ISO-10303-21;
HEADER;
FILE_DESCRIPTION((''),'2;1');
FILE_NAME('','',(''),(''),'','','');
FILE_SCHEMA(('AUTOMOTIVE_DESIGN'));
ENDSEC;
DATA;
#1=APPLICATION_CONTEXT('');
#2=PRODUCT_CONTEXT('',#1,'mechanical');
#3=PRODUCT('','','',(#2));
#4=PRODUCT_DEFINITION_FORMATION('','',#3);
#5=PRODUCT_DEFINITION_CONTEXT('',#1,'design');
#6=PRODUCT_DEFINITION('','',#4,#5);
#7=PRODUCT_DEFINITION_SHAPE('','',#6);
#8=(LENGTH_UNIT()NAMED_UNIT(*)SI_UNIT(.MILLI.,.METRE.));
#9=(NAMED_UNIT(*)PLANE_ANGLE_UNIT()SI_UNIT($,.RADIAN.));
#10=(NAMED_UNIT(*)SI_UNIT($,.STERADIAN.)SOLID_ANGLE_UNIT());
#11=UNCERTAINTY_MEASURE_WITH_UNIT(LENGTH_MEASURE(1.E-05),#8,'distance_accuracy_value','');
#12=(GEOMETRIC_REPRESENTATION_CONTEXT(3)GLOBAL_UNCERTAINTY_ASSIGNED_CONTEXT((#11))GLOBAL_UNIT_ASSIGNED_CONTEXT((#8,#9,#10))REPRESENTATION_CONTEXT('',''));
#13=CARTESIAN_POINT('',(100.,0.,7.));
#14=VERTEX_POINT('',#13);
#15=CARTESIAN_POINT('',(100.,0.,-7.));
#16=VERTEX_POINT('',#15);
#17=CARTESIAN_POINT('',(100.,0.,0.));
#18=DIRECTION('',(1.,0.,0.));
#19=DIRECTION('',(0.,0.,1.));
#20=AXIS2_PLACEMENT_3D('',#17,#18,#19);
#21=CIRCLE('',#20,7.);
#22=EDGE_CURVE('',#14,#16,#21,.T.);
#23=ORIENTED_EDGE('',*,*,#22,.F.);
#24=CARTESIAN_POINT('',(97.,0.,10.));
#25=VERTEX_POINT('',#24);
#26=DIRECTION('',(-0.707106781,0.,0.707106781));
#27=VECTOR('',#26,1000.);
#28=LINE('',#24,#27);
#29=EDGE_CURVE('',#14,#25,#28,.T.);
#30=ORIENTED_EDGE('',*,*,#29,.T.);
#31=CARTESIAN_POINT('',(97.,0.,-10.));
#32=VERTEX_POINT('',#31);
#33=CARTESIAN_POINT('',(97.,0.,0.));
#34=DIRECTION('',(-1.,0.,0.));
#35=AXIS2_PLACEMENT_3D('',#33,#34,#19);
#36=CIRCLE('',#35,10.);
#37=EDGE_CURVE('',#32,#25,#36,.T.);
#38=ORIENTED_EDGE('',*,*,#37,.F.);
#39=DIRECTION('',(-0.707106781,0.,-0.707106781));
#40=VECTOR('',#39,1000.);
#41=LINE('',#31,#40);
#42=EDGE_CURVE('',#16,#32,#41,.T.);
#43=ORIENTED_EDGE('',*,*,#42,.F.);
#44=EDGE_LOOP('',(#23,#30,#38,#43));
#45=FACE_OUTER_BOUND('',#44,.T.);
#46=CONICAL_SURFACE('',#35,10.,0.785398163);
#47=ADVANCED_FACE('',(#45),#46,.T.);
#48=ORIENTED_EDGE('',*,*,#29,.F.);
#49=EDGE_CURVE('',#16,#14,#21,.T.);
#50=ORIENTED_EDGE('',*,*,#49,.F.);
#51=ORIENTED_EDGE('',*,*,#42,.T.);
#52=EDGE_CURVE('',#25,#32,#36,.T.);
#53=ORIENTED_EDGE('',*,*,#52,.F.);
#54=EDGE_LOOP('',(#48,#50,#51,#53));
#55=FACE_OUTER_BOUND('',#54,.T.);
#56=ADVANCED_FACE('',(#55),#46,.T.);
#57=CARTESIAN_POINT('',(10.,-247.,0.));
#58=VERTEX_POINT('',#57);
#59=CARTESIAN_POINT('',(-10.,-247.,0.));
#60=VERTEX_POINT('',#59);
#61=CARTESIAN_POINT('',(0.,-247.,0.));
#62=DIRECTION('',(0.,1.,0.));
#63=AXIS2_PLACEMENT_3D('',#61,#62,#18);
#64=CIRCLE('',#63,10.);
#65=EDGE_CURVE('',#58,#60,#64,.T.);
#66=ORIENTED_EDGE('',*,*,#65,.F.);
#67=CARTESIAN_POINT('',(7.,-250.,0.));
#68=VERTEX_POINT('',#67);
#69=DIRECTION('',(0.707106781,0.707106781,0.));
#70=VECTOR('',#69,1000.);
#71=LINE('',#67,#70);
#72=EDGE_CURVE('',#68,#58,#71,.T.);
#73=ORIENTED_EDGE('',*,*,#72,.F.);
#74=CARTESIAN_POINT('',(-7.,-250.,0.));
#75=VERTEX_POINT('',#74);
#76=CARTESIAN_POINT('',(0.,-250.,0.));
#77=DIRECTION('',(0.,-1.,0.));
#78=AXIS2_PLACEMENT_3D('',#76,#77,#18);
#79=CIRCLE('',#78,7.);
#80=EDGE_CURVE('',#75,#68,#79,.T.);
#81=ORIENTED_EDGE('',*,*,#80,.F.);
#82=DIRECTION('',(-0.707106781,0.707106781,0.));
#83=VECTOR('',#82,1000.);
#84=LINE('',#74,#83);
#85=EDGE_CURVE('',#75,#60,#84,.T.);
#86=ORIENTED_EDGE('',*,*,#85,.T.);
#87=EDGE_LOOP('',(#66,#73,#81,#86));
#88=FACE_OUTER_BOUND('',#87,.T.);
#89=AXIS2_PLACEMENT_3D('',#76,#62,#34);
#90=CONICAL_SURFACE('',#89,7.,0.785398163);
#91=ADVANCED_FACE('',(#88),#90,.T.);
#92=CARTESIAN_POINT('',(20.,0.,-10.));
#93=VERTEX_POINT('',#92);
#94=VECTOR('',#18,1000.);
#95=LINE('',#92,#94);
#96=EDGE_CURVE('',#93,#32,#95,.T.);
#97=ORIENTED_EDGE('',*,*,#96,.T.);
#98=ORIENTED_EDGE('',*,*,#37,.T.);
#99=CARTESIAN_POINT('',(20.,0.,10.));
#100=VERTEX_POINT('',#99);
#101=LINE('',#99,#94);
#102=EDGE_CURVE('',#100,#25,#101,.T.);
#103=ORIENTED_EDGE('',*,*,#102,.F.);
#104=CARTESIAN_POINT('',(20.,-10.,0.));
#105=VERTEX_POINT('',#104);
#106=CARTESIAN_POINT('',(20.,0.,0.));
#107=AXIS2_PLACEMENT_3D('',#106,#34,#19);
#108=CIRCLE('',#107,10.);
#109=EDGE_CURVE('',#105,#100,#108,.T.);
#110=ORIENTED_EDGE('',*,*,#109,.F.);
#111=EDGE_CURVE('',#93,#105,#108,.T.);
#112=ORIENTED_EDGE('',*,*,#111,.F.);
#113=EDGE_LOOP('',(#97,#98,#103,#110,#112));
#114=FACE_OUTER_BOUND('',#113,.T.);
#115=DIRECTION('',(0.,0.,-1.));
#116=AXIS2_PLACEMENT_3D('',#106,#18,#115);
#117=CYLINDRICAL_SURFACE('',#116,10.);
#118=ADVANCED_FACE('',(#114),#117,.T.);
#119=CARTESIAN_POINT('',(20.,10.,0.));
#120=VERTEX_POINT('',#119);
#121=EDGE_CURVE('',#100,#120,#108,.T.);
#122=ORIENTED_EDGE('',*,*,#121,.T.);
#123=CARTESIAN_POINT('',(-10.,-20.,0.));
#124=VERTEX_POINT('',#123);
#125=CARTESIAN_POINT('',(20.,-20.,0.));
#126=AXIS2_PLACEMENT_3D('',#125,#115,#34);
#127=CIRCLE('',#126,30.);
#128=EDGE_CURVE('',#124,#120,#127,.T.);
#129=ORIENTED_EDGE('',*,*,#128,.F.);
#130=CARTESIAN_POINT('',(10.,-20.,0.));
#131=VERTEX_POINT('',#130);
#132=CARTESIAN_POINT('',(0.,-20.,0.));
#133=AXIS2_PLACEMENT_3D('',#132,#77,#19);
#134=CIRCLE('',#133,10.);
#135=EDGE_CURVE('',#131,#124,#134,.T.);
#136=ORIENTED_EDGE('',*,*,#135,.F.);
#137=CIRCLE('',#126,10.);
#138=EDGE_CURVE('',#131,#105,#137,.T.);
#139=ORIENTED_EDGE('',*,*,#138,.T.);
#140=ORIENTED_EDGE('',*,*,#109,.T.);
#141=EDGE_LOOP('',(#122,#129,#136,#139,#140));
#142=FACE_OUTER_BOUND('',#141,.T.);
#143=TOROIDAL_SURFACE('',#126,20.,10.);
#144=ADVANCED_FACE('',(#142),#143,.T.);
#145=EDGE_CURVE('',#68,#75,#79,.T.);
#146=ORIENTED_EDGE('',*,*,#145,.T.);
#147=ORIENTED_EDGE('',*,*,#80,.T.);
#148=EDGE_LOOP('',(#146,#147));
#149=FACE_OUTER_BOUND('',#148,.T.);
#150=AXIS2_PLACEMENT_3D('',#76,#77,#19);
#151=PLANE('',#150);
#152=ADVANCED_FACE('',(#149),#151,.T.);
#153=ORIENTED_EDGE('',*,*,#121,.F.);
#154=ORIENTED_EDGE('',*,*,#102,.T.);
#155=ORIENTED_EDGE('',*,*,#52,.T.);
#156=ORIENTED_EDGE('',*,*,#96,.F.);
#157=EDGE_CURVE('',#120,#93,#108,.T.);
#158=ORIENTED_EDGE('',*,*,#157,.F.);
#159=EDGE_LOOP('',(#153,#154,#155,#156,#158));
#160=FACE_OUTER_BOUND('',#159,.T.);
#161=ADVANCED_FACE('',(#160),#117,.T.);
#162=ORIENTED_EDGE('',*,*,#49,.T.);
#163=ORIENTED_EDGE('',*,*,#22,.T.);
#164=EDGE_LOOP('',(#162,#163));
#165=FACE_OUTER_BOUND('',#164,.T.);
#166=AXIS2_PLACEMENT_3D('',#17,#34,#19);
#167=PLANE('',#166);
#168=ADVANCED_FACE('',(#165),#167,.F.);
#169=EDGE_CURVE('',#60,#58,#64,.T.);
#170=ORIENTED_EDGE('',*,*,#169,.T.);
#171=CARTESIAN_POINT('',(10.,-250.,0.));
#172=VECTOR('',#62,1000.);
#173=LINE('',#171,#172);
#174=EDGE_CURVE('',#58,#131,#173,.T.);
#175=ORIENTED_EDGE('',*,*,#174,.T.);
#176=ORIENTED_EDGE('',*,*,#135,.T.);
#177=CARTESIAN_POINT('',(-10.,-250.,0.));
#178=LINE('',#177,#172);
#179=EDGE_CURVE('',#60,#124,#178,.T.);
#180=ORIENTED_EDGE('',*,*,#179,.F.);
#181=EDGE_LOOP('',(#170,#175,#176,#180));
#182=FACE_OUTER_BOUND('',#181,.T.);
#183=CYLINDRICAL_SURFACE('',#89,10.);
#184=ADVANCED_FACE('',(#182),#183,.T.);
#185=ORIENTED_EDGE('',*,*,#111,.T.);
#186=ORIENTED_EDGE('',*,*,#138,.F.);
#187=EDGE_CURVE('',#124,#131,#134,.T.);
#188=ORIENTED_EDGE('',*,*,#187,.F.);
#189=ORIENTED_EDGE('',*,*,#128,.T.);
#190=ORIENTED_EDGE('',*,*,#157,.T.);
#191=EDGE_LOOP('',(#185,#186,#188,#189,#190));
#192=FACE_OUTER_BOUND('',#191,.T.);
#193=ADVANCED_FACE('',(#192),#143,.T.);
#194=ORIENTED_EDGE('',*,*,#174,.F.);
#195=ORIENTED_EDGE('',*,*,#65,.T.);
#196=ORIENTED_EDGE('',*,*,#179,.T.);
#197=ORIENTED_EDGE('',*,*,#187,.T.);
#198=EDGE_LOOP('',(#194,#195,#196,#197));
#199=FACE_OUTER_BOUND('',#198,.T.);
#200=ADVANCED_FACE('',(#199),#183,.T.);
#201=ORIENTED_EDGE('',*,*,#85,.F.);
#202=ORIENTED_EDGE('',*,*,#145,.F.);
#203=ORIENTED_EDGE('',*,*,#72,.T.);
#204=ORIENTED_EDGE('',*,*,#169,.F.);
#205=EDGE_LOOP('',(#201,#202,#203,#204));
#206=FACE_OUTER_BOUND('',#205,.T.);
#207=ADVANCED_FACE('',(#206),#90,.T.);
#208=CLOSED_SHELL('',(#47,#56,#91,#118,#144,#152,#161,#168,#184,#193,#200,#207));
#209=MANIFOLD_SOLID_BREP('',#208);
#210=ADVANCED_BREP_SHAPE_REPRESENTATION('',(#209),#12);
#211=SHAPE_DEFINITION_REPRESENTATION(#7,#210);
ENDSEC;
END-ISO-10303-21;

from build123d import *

# Parameters (mm, degrees)
SWEEP_1_PROFILE_R = 10
CHAMFER_1_SIZE    = 3
CHAMFER_2_SIZE    = 3


with BuildPart() as part:
    # 扫描1: sweep along a path in 草图1
    with BuildLine(Plane.XY) as sweep_1_path:
        Line((0, -250), (0, -20))
        ThreePointArc((0, -20), (5.857864376, -5.857864376), (20, 0))
        Line((20, 0), (100, 0))
    # 扫描1 profile (on start of the path) → 扫描1 (sweep)
    with BuildSketch(Plane(origin=(0, -250, 0), x_dir=(1, 0, 0), z_dir=(0, 1, 0))):
        Circle(SWEEP_1_PROFILE_R)
    sweep(path=sweep_1_path.line)

    # 倒角1
    chamfer_1_edges = [part.edges().sort_by_distance(p)[0] for p in [
        (-10, -250, 0),
    ]]
    chamfer(chamfer_1_edges, length=CHAMFER_1_SIZE)

    # 倒角2
    chamfer_2_edges = [part.edges().sort_by_distance(p)[0] for p in [
        (100, 10, 0),
    ]]
    chamfer(chamfer_2_edges, length=CHAMFER_2_SIZE)


solid = part.part
